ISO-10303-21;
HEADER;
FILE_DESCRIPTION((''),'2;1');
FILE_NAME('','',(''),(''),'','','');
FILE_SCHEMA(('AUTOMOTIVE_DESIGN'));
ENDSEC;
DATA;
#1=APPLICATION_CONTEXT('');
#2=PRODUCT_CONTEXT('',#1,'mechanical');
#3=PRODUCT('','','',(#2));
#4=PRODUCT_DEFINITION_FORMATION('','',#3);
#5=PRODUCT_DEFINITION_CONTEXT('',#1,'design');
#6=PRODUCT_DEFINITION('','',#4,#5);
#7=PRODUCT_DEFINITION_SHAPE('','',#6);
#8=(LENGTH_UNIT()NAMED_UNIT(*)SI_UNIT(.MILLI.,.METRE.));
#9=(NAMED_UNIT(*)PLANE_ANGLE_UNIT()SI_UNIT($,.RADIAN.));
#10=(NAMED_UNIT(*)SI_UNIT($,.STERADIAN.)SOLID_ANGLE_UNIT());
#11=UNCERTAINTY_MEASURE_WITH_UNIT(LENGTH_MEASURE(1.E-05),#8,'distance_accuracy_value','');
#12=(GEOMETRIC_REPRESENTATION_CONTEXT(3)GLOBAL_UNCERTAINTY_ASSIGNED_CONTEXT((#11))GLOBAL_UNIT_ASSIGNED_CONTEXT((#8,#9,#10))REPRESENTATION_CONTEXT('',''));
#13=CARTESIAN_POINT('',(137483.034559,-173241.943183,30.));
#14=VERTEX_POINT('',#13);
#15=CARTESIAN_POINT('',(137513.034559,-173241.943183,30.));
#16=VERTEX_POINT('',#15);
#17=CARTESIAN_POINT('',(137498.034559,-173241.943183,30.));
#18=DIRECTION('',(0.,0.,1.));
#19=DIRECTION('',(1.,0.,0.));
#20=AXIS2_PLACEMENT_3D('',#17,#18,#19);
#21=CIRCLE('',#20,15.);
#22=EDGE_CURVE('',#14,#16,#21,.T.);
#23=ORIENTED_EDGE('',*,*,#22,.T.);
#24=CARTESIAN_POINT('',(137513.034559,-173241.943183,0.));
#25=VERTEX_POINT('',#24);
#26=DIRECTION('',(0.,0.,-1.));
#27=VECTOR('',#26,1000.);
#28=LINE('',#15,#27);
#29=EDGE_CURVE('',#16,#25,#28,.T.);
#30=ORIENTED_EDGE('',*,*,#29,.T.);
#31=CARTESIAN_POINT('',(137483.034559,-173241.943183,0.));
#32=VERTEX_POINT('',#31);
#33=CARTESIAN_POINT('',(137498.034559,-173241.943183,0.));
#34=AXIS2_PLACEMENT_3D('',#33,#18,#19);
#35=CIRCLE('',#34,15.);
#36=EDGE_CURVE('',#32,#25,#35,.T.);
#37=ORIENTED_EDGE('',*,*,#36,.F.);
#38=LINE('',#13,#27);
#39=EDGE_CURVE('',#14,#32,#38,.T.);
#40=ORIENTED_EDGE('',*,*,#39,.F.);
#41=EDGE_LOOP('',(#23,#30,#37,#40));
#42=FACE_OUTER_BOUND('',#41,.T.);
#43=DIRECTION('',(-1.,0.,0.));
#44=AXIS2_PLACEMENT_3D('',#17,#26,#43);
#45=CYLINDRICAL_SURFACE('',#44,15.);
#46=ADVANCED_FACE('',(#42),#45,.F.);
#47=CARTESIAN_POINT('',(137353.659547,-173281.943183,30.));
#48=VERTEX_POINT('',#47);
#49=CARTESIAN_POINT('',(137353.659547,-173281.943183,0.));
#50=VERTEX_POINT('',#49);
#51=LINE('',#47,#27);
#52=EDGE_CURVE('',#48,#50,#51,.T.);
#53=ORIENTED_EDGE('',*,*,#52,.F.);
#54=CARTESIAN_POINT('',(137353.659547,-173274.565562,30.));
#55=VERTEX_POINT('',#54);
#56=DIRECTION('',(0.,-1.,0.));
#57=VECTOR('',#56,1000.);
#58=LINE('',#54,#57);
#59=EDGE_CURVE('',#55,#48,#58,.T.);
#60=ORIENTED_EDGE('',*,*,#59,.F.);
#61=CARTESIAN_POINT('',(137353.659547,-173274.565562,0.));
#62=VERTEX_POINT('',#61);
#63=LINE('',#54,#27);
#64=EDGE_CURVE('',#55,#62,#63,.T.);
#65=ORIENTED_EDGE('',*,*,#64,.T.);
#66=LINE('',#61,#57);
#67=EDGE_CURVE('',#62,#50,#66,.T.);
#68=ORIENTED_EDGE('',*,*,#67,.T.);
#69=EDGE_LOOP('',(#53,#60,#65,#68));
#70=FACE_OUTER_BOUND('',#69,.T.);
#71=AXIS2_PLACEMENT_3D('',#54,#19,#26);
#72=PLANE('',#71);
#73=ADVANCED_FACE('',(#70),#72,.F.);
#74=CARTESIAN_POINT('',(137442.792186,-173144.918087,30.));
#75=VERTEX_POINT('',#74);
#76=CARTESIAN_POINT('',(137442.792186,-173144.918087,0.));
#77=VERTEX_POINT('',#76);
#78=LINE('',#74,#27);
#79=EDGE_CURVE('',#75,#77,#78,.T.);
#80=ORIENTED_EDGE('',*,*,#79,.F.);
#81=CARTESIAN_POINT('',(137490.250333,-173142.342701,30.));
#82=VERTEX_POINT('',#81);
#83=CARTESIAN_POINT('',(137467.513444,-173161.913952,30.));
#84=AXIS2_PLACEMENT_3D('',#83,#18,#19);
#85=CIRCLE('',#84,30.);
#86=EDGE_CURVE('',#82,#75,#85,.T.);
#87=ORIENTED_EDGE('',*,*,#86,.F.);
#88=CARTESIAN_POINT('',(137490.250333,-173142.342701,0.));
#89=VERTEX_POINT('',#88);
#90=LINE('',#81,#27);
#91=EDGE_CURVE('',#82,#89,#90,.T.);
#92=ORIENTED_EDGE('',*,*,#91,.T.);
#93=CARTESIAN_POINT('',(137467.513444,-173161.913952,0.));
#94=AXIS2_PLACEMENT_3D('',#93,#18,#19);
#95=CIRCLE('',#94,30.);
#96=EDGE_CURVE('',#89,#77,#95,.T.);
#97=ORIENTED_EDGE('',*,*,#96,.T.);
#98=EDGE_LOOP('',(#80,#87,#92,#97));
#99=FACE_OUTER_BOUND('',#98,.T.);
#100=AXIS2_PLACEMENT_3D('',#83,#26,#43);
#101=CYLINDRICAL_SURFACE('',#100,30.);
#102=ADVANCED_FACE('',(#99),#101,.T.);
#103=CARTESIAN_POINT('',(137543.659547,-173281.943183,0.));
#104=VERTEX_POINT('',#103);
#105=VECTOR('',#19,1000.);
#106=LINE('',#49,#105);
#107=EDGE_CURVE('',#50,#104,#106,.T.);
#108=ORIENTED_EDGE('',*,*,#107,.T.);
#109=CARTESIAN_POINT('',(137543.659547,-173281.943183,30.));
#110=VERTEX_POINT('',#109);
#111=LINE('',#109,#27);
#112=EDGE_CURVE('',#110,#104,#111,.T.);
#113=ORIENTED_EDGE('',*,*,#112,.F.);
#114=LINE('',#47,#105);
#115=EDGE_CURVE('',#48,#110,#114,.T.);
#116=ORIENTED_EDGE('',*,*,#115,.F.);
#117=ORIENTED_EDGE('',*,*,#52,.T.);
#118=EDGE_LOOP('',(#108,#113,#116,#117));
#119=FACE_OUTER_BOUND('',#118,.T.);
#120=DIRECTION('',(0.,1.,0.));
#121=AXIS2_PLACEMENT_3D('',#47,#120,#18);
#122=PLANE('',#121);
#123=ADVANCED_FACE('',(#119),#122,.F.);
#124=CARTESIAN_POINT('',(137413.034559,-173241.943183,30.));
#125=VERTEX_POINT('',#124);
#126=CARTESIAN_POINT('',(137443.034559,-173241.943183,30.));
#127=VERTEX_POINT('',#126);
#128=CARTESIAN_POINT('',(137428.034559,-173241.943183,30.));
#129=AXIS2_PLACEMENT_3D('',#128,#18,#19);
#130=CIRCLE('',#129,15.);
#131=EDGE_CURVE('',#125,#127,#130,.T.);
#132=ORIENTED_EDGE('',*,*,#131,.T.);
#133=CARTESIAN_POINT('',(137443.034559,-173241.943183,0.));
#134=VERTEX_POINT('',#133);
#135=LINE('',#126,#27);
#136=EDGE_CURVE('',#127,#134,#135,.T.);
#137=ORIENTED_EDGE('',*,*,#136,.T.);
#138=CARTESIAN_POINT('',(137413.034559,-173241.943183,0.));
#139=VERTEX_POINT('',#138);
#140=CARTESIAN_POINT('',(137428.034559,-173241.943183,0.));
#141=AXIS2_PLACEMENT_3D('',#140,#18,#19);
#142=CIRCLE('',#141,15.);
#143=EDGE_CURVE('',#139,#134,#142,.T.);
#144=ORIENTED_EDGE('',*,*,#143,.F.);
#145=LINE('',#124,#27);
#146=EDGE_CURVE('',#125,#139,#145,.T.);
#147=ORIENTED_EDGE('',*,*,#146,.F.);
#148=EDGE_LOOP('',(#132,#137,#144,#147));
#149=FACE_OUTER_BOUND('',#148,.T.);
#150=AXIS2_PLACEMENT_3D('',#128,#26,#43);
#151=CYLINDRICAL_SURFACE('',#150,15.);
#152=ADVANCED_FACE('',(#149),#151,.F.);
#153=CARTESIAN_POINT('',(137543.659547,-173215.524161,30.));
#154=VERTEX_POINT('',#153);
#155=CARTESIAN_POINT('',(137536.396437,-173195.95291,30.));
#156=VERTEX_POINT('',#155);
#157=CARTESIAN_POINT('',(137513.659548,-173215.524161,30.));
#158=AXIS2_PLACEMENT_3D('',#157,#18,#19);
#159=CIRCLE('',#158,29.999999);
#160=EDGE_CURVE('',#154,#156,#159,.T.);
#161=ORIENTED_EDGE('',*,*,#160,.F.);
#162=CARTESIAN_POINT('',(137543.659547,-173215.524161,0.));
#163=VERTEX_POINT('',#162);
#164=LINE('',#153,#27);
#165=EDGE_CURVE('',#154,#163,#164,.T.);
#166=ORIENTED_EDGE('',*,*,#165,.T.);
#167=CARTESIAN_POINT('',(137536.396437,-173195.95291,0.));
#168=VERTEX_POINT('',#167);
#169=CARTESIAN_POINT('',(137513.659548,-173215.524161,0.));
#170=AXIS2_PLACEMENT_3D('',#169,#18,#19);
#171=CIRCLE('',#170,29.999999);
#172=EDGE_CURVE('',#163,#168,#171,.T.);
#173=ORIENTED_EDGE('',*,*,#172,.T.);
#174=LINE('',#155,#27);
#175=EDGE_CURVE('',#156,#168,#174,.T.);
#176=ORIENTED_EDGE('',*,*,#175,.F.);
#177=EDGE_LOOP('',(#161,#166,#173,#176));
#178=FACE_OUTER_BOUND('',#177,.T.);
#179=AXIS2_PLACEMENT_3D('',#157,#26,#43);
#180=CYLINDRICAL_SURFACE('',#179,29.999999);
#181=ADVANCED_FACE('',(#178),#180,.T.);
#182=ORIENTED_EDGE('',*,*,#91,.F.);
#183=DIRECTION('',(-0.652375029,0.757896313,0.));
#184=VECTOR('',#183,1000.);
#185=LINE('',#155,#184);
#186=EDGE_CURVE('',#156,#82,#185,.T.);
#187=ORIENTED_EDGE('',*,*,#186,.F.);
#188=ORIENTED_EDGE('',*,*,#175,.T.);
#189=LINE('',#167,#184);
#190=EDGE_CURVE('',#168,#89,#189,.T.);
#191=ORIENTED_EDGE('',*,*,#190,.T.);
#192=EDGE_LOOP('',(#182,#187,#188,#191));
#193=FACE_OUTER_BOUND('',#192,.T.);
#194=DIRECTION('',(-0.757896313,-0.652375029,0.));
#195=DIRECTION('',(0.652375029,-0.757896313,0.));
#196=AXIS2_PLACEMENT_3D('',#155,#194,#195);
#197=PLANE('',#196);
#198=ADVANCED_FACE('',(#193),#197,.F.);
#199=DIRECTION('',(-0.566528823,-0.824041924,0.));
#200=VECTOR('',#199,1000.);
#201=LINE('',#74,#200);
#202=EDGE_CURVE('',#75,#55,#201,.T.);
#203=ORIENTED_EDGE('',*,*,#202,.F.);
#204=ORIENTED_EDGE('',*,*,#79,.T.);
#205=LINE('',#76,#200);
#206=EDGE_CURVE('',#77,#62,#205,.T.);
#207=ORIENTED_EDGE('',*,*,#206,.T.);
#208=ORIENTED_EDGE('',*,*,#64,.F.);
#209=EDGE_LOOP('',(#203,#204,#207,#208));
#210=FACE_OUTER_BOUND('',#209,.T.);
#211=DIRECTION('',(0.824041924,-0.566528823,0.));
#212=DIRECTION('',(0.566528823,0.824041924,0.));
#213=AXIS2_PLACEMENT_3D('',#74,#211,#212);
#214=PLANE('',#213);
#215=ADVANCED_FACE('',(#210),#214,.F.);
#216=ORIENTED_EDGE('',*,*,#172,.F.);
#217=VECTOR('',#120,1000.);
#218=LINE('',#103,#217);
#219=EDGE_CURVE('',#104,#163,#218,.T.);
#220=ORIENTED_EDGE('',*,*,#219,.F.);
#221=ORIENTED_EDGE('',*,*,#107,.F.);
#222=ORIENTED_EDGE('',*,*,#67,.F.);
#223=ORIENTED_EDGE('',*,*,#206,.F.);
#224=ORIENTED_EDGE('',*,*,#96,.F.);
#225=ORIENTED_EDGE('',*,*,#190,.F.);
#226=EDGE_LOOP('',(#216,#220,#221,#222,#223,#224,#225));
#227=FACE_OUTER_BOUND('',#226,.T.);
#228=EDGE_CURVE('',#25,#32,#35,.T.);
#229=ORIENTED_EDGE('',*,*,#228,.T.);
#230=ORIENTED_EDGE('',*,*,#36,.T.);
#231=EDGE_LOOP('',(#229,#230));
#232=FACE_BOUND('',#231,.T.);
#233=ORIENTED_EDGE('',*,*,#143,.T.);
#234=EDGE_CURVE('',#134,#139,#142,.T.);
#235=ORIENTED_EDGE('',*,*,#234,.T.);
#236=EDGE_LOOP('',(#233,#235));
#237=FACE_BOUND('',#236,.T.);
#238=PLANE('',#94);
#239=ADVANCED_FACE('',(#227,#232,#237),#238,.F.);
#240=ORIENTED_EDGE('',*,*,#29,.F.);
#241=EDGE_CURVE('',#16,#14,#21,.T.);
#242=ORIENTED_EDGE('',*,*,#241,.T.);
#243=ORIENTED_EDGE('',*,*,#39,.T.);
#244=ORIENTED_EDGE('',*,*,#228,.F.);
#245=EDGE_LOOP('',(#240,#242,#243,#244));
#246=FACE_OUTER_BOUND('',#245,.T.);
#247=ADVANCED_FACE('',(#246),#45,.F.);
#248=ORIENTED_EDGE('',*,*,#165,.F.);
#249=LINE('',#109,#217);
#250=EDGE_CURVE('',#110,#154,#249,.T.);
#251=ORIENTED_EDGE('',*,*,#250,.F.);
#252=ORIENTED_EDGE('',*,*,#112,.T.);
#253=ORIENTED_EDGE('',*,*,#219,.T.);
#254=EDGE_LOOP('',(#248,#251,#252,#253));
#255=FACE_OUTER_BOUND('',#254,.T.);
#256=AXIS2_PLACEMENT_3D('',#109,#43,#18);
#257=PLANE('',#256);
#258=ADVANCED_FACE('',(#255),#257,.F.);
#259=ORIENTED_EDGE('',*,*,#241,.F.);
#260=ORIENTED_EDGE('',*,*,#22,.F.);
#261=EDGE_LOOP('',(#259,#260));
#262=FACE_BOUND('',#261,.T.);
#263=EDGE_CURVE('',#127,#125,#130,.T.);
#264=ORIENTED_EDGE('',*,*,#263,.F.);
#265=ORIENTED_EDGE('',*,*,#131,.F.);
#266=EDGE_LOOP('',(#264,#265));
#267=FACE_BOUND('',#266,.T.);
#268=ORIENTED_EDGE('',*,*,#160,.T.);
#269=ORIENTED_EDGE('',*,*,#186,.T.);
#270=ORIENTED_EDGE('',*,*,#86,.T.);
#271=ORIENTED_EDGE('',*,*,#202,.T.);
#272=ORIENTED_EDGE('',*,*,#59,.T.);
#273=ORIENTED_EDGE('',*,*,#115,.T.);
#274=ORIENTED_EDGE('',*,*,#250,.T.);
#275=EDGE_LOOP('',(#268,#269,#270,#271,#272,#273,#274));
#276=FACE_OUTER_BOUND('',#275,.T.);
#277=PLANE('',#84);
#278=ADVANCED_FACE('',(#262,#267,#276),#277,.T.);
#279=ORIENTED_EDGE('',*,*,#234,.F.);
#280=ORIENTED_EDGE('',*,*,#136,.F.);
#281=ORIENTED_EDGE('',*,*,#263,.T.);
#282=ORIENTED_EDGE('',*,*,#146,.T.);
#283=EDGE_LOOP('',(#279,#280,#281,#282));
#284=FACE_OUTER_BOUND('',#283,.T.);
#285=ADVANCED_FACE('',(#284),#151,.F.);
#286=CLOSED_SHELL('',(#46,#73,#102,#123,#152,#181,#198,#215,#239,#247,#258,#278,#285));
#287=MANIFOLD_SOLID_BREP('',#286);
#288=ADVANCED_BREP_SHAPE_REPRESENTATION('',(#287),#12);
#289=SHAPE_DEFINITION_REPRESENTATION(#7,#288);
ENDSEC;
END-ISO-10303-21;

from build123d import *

# Parameters (mm, degrees)
SKETCH1_R           = 15
BOSS_EXTRUDE1_DEPTH = 30


with BuildPart() as part:
    # Sketch1 → Boss-Extrude1 (new body)
    with BuildSketch(Plane.XY):
        with BuildLine():
            Line((137442.792186055, -173144.918087479), (137353.659547419, -173274.56556186))
            Line((137353.659547419, -173274.56556186), (137353.659547419, -173281.943182873))
            Line((137353.659547419, -173281.943182873), (137543.659547419, -173281.943182873))
            Line((137543.659547419, -173281.943182873), (137543.659547419, -173215.524161381))
            ThreePointArc((137543.659547419, -173215.524161381), (137541.785217916, -173205.086409641), (137536.396436674, -173195.952910355))
            Line((137536.396436674, -173195.952910355), (137490.250333171, -173142.34270129))
            ThreePointArc((137490.250333171, -173142.34270129), (137465.887841454, -173131.958027607), (137442.792186055, -173144.918087479))
        make_face()
        with Locations((137498.03455904, -173241.943182873)):
            Circle(SKETCH1_R, mode=Mode.SUBTRACT)
        with Locations((137428.03455904, -173241.943182873)):
            Circle(SKETCH1_R, mode=Mode.SUBTRACT)
    extrude(amount=BOSS_EXTRUDE1_DEPTH)


solid = part.part
